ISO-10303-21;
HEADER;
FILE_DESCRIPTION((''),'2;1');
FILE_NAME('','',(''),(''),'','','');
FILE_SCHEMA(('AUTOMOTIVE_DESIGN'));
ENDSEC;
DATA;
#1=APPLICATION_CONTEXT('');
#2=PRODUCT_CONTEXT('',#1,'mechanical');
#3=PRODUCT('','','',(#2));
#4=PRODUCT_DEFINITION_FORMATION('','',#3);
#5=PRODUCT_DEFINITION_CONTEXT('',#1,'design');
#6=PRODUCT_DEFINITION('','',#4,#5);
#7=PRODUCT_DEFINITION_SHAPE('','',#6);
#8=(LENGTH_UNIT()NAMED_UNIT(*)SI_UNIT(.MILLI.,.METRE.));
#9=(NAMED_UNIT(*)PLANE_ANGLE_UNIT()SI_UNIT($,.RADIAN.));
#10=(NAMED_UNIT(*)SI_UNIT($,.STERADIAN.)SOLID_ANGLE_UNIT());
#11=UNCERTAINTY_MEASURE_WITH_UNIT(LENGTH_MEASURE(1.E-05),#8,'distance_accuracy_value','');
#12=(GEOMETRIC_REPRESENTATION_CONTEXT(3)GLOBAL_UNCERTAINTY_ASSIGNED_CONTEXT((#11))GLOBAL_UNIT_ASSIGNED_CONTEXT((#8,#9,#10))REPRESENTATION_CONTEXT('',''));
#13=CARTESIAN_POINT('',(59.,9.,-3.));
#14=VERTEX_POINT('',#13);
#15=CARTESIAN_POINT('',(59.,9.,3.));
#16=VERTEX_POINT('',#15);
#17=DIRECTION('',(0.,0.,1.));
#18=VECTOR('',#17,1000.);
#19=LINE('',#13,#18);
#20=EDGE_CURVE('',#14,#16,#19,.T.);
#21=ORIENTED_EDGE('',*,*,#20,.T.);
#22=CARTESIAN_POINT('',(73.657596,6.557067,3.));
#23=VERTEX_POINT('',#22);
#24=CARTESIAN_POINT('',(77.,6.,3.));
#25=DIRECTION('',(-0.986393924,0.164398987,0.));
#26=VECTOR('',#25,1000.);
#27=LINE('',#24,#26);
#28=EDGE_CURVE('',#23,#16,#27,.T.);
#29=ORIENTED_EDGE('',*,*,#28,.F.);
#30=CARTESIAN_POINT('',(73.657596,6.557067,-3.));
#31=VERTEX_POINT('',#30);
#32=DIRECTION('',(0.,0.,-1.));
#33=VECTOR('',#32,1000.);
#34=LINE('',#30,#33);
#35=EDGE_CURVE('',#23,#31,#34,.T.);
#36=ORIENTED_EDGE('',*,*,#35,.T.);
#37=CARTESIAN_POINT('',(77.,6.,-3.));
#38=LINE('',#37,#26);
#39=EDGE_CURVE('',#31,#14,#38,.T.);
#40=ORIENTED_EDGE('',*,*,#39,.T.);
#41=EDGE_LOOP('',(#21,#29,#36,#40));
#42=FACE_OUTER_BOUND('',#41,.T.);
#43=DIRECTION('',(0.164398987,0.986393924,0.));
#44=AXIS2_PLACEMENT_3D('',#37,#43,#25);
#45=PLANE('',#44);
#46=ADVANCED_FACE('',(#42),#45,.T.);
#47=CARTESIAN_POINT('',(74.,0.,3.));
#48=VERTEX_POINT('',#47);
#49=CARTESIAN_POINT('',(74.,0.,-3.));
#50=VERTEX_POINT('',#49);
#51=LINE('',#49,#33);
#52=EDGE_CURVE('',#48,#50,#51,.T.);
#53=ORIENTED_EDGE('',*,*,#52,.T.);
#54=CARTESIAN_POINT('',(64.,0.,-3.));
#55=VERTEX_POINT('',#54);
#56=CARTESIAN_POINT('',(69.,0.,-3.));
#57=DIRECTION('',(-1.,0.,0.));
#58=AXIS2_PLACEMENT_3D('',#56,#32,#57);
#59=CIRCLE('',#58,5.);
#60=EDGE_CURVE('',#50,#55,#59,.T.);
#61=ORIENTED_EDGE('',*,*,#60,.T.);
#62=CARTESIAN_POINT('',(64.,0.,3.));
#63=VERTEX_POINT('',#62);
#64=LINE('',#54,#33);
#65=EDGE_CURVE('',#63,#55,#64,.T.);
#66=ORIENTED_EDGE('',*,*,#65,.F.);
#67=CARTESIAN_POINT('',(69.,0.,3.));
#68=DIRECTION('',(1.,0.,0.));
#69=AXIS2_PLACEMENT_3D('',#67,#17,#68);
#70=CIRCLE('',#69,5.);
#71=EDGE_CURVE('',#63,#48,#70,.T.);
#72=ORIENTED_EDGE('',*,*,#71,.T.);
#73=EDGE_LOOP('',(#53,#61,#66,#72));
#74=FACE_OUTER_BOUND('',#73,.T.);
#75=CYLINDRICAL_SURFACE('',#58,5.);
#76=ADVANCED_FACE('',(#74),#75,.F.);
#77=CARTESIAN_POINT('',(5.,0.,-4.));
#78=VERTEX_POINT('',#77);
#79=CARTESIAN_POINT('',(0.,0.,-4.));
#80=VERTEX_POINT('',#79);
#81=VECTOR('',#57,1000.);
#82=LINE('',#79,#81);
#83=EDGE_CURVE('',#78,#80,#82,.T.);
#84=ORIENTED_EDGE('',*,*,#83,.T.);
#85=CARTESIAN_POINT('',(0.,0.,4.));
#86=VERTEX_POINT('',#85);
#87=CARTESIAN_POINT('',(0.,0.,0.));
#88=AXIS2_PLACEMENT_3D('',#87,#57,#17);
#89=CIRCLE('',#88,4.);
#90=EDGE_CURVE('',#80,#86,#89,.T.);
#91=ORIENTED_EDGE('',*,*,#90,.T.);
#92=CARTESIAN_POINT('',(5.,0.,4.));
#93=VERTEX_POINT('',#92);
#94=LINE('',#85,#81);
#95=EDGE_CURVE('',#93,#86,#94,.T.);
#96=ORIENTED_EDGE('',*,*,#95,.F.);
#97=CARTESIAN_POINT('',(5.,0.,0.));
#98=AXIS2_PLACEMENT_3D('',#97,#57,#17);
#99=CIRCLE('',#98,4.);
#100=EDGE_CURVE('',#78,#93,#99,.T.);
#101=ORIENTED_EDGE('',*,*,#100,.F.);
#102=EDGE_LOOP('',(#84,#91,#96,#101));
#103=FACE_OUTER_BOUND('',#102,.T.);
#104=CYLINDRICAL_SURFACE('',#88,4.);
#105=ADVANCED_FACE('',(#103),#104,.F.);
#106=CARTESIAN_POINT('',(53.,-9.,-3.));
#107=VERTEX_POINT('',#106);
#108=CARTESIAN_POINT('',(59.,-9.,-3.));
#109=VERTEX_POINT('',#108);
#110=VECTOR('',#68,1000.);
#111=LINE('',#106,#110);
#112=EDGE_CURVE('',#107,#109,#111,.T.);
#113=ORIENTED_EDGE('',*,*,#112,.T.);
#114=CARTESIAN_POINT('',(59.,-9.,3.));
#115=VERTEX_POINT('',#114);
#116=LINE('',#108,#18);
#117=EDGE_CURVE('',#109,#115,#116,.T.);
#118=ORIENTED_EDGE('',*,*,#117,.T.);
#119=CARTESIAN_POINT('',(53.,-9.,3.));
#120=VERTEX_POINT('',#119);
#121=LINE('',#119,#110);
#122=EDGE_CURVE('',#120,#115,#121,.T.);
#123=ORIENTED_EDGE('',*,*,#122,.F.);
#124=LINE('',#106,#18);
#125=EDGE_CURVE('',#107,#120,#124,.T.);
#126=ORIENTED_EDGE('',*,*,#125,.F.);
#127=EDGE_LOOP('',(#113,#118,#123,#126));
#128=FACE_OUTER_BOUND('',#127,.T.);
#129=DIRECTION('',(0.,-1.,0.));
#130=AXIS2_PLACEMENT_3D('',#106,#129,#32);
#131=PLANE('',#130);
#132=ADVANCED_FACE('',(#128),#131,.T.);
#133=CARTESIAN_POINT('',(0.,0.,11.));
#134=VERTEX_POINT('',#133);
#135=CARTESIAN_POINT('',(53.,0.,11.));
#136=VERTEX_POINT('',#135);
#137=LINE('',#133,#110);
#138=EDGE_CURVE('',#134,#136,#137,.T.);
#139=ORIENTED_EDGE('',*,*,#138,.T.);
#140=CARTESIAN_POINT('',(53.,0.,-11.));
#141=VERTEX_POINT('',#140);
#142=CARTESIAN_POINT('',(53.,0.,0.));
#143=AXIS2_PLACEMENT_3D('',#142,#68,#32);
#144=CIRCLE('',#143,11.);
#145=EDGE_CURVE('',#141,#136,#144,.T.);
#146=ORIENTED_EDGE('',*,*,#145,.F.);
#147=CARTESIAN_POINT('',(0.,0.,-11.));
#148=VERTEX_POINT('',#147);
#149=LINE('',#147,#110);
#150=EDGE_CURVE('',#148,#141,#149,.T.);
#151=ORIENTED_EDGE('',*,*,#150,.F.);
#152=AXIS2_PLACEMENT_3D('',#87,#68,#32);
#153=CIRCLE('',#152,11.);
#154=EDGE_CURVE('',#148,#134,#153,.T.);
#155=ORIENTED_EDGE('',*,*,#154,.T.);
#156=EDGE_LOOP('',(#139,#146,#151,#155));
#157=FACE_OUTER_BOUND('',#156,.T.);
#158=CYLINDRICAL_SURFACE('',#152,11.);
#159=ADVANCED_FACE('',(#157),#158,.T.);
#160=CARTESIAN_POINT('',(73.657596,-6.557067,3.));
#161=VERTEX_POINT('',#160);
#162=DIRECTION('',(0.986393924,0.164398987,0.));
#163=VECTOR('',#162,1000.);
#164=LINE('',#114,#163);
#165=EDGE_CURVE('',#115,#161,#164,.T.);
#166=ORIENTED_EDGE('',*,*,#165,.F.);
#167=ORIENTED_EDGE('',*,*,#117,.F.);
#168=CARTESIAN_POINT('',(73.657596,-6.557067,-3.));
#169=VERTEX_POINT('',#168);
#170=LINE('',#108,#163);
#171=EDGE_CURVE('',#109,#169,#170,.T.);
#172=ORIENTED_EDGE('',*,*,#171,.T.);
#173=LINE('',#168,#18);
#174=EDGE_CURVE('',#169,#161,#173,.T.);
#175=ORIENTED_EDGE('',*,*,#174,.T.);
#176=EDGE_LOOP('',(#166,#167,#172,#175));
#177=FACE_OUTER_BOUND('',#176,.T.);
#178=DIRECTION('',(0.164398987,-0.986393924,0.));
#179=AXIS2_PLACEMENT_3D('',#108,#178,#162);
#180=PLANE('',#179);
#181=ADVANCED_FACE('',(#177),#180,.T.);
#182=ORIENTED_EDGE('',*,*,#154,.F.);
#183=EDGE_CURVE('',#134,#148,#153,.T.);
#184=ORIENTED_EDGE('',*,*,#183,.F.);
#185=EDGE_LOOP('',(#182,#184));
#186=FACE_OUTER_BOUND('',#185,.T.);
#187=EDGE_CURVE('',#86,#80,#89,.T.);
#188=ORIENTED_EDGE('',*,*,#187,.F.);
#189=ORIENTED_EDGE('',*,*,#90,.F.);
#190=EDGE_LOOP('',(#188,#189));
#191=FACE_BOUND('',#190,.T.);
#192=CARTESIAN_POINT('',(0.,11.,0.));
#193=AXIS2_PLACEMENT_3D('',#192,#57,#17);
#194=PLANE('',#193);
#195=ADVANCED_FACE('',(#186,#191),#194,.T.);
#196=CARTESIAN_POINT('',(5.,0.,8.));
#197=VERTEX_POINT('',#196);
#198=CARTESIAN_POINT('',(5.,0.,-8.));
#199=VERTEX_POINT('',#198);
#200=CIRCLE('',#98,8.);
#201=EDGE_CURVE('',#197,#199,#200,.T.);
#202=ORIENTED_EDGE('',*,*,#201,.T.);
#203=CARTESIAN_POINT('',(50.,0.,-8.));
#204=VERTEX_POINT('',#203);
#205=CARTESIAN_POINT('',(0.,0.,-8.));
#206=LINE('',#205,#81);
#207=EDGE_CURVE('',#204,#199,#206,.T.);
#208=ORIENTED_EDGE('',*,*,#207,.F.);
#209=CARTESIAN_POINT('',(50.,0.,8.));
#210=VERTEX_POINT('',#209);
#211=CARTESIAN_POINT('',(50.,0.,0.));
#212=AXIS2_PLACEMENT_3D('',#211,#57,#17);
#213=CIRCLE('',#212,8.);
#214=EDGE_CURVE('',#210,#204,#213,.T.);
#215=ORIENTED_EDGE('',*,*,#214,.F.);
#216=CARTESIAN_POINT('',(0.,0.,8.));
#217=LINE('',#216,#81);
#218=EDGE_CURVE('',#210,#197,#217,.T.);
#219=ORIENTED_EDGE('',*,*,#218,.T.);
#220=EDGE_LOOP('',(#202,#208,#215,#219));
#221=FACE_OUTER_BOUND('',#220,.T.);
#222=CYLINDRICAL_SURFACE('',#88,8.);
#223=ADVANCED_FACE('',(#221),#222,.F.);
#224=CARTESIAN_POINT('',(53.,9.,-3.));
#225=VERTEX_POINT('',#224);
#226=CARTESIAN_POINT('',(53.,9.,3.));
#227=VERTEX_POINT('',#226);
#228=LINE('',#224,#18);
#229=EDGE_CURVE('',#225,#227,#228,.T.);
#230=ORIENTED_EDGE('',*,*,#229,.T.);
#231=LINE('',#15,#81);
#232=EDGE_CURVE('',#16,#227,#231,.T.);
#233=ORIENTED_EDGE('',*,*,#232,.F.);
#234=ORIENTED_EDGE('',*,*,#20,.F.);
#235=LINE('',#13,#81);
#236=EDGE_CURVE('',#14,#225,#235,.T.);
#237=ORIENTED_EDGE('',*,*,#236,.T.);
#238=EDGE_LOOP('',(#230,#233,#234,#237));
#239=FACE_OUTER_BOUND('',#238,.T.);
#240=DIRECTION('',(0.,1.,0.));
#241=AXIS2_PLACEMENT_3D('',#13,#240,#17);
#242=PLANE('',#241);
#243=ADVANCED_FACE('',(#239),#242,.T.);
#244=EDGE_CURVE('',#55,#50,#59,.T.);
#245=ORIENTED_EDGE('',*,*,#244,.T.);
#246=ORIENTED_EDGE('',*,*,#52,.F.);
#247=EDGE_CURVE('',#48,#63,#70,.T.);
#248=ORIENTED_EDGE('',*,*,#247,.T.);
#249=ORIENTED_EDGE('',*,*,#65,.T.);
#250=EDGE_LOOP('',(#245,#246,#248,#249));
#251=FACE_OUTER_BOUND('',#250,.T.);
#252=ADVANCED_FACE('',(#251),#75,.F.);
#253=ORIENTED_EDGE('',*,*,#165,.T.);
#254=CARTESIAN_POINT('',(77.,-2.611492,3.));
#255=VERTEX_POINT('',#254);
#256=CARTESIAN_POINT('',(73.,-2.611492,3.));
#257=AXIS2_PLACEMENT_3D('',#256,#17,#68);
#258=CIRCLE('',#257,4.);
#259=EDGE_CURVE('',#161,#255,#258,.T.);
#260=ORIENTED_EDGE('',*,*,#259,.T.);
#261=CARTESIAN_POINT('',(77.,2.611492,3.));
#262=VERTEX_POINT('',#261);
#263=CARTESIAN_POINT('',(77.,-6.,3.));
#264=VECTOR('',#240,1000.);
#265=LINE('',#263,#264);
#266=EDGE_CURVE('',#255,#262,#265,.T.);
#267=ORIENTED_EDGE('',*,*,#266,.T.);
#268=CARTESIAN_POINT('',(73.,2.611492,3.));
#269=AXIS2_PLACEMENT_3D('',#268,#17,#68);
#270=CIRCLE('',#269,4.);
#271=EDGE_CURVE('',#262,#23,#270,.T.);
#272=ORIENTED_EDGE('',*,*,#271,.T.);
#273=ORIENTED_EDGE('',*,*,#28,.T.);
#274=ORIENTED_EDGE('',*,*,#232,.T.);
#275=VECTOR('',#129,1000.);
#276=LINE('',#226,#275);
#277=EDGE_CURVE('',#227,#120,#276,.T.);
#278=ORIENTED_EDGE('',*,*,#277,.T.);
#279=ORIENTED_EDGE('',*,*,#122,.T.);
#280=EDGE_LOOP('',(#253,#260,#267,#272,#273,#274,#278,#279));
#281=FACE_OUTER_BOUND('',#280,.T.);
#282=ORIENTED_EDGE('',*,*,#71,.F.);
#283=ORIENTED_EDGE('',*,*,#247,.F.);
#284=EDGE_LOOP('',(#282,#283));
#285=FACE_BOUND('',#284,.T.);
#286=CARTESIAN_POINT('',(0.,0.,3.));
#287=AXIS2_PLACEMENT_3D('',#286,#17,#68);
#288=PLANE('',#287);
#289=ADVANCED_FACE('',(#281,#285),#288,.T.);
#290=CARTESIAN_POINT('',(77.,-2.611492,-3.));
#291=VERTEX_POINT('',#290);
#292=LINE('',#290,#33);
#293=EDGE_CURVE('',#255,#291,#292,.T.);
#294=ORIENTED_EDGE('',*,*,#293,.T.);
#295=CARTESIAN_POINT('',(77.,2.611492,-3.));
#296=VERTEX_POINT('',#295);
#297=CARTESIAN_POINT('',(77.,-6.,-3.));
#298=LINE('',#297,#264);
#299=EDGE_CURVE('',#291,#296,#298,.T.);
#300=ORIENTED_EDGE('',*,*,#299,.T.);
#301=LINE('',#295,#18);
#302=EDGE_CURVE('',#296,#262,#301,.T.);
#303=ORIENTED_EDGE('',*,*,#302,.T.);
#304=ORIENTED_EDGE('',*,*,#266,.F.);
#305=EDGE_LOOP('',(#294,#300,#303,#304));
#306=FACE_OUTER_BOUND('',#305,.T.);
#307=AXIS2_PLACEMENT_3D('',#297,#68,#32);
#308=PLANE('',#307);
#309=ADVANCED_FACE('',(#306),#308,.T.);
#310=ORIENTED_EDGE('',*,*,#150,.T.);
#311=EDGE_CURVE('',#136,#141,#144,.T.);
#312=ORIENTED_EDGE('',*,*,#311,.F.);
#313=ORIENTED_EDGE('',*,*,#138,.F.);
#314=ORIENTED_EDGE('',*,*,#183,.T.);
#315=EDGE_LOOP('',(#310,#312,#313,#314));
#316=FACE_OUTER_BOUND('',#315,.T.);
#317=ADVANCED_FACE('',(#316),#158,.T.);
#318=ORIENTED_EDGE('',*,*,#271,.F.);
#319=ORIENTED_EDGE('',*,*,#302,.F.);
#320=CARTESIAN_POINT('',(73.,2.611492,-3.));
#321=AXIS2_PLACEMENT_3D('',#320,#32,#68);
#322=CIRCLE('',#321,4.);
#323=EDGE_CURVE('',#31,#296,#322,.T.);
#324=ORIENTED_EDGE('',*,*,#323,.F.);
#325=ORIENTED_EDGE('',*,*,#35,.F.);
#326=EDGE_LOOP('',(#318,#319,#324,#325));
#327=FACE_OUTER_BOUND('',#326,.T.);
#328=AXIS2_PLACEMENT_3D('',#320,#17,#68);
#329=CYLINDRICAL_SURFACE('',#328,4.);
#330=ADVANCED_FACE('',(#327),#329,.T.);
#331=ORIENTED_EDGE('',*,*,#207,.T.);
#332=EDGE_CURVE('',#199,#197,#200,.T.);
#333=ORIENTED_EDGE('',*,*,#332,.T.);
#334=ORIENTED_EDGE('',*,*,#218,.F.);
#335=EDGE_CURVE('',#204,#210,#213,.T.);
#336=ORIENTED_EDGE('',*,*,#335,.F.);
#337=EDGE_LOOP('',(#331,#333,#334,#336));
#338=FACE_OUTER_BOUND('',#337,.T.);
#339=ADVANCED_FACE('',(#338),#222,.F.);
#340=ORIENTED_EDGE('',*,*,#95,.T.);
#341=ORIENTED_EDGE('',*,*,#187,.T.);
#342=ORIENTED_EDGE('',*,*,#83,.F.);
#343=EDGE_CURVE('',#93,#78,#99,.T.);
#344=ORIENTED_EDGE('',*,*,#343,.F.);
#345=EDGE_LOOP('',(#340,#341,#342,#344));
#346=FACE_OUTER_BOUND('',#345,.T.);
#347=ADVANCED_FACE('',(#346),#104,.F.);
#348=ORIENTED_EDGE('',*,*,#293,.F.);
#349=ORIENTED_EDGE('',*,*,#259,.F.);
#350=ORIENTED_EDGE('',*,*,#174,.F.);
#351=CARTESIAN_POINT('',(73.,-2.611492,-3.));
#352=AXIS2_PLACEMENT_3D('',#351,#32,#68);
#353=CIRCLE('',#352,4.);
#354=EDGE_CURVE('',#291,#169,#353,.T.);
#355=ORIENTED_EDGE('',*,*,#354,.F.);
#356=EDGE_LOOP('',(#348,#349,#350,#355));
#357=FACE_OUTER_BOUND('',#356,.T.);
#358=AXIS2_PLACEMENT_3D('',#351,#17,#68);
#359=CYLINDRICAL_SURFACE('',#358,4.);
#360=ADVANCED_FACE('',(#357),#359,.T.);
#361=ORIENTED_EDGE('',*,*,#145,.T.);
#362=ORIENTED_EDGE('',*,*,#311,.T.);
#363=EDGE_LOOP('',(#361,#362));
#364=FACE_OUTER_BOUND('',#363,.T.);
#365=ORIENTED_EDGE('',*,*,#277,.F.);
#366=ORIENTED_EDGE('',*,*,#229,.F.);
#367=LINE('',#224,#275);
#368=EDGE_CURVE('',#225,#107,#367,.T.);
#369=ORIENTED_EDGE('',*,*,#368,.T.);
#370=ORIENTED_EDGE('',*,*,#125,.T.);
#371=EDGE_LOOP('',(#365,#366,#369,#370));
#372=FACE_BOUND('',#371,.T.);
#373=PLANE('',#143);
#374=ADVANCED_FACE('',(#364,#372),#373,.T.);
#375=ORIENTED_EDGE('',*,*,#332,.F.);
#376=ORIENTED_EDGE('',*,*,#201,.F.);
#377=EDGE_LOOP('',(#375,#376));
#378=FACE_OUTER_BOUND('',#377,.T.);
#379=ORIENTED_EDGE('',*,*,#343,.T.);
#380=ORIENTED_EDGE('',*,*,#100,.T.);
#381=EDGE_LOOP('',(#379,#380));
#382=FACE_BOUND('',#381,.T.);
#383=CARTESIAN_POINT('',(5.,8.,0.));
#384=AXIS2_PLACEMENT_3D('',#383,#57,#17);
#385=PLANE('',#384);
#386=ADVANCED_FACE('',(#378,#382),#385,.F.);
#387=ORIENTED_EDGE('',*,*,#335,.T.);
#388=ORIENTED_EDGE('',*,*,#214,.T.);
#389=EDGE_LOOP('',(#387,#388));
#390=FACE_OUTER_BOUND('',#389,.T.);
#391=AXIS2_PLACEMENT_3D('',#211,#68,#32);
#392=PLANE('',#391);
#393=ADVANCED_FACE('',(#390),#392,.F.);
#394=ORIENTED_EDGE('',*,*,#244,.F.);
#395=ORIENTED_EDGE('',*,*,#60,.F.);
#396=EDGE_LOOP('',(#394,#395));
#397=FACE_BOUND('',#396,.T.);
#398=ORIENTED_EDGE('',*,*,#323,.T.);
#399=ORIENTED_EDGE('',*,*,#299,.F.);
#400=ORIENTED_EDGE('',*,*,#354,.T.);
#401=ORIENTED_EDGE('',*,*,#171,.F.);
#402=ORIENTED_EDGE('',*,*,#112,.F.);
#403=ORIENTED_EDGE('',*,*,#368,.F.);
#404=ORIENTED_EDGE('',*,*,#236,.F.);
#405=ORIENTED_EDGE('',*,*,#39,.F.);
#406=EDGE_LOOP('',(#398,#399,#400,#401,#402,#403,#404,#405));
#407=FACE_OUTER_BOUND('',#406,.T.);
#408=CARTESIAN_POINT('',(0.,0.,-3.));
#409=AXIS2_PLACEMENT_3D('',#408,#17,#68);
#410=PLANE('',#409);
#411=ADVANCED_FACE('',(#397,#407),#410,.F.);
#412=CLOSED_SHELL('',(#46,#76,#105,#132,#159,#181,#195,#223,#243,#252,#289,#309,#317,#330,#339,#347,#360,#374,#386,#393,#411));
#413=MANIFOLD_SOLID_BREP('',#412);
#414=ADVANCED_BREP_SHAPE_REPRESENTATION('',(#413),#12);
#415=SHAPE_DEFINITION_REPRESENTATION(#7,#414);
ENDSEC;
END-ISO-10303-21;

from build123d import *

# Parameters (mm, degrees)
SKETCH1_W                      = 53
SKETCH1_H                      = 11
BOSS_EXTRUDE1_DEPTH            = 6
F_10_0_10_DIAMETER_HOLE1_D     = 10
F_10_0_10_DIAMETER_HOLE1_DEPTH = 14
FILLET1_R                      = 4


with BuildPart() as part:
    # Sketch1 → Revolve1 (revolve)
    with BuildSketch(Plane.XY, mode=Mode.PRIVATE) as revolve1_sk:
        with Locations((26.5, 5.5)):
            Rectangle(SKETCH1_W, SKETCH1_H)
    revolve(revolve1_sk.sketch.rotate(Axis((0, 0, 0), (1, 0, 0)), 270), axis=Axis((0, 0, 0), (1, 0, 0)))

    # Sketch2 → Boss-Extrude1 (add)
    with BuildSketch(Plane.XY.offset(3)):
        Polygon((77, -6), (77, 6), (59, 9), (53, 9), (53, -9), (59, -9), align=None)
    extrude(amount=-BOSS_EXTRUDE1_DEPTH)

    # Ø10.0 (10) Diameter Hole1
    with Locations(Plane(origin=(0, 0, -3), x_dir=(-1, 0, 0), z_dir=(0, 0, -1))):
        with Locations((-69, 0)):
            Hole(F_10_0_10_DIAMETER_HOLE1_D / 2, depth=F_10_0_10_DIAMETER_HOLE1_DEPTH)

    # Sketch5 → CBORE for M13 SHSS1 (revolve, cut)
    with BuildSketch(Plane.ZX):
        Polygon((0, 0), (0, 50), (8, 50), (8, 5), (4, 5), (4, 0), align=None)
    revolve(axis=Axis((-6.35, 0, 0), (1, 0, 0)), mode=Mode.SUBTRACT)

    # Fillet1
    fillet1_edges = [part.edges().sort_by_distance(p)[0] for p in [
        (77, -6, 0),
        (77, 6, 0),
    ]]
    fillet(fillet1_edges, radius=FILLET1_R)


solid = part.part
